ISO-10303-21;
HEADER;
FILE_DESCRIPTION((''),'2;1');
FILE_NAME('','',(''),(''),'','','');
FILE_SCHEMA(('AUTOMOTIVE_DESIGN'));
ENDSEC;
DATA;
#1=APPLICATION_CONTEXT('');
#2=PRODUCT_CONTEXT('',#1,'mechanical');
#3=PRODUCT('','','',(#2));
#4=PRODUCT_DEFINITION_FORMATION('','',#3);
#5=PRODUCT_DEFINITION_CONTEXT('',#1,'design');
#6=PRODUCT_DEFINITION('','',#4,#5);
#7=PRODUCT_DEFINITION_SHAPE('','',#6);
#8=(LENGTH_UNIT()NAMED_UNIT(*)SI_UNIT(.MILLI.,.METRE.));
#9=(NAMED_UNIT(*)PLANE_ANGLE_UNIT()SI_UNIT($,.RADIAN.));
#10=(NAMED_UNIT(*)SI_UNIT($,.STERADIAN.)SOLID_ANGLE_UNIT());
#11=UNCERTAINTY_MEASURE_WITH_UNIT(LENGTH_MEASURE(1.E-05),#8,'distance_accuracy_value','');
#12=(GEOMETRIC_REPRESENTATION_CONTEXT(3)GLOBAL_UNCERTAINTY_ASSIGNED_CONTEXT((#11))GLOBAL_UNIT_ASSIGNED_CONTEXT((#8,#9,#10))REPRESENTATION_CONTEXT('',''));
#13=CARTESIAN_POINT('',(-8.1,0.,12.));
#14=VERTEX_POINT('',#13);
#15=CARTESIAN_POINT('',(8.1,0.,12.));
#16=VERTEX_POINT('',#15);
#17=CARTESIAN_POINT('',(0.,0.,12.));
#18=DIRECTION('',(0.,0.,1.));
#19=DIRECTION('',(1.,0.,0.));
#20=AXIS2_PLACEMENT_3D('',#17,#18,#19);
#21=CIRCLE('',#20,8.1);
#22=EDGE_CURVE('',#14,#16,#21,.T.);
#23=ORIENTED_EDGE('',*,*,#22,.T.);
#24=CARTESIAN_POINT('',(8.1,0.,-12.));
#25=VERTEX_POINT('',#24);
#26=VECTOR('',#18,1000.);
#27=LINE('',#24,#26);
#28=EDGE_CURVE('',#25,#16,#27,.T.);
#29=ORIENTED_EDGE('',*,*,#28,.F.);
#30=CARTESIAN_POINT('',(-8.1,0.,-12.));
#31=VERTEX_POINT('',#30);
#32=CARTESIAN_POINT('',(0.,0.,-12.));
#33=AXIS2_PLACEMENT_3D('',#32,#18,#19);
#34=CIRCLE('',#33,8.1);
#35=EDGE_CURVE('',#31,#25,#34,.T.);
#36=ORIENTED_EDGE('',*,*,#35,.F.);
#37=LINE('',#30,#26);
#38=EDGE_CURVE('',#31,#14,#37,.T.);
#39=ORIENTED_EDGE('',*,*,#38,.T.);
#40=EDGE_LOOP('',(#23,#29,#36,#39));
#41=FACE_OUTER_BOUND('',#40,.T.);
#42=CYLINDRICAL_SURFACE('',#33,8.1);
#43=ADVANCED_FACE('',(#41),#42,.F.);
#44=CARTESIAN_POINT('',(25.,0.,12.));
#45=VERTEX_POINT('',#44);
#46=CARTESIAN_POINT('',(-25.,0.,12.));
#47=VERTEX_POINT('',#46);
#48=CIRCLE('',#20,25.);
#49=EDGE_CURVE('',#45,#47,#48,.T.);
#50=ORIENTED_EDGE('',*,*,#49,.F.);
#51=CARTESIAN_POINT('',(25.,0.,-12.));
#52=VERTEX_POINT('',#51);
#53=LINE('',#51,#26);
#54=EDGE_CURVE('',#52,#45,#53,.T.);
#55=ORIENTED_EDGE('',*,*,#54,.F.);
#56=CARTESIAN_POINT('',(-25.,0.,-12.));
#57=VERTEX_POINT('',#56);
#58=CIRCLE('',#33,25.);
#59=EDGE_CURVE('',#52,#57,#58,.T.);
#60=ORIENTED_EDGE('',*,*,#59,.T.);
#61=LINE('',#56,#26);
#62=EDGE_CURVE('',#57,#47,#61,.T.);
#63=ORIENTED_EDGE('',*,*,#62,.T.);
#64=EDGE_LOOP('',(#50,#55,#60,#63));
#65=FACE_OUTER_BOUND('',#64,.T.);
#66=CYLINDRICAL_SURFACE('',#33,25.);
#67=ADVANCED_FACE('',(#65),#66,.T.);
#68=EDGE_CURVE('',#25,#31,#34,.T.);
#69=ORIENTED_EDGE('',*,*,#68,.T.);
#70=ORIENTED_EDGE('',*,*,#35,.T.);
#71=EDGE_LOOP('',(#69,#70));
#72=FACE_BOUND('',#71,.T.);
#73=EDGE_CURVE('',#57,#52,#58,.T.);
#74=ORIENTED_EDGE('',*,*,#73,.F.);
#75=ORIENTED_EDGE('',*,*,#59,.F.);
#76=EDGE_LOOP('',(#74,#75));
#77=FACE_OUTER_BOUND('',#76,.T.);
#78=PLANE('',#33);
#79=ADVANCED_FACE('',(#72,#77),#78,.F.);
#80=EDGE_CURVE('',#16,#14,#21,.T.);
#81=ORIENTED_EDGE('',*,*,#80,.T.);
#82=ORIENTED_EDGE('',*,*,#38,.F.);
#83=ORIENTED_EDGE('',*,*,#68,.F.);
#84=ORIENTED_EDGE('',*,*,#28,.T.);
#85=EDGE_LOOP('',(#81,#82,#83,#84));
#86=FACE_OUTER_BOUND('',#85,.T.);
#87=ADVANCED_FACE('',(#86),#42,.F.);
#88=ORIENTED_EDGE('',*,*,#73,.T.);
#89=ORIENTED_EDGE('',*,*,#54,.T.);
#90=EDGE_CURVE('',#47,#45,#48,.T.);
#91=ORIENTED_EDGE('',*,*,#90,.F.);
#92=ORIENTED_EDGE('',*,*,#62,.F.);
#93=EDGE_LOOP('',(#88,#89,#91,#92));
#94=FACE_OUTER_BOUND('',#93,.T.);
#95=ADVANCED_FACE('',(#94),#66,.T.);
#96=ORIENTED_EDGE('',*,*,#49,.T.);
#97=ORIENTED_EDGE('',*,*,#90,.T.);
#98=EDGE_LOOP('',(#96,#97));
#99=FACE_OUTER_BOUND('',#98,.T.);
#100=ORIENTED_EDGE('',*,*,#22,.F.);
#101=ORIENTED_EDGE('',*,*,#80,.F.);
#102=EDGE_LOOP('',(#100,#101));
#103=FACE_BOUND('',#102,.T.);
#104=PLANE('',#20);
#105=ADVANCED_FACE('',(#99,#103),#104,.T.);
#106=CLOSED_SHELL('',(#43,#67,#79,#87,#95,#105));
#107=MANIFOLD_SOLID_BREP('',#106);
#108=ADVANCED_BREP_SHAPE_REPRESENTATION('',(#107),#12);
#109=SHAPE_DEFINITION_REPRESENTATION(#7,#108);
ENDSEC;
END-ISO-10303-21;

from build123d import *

# Parameters (mm, degrees)
SKETCH_1_R      = 25
SKETCH_1_R_2    = 8.1
EXTRUDE_1_DEPTH = 12


with BuildPart() as part:
    # 草图1 → 凸台-拉伸1 (new, symmetric)
    with BuildSketch(Plane.XY):
        Circle(SKETCH_1_R)
        Circle(SKETCH_1_R_2, mode=Mode.SUBTRACT)
    extrude(amount=EXTRUDE_1_DEPTH, both=True)


solid = part.part
